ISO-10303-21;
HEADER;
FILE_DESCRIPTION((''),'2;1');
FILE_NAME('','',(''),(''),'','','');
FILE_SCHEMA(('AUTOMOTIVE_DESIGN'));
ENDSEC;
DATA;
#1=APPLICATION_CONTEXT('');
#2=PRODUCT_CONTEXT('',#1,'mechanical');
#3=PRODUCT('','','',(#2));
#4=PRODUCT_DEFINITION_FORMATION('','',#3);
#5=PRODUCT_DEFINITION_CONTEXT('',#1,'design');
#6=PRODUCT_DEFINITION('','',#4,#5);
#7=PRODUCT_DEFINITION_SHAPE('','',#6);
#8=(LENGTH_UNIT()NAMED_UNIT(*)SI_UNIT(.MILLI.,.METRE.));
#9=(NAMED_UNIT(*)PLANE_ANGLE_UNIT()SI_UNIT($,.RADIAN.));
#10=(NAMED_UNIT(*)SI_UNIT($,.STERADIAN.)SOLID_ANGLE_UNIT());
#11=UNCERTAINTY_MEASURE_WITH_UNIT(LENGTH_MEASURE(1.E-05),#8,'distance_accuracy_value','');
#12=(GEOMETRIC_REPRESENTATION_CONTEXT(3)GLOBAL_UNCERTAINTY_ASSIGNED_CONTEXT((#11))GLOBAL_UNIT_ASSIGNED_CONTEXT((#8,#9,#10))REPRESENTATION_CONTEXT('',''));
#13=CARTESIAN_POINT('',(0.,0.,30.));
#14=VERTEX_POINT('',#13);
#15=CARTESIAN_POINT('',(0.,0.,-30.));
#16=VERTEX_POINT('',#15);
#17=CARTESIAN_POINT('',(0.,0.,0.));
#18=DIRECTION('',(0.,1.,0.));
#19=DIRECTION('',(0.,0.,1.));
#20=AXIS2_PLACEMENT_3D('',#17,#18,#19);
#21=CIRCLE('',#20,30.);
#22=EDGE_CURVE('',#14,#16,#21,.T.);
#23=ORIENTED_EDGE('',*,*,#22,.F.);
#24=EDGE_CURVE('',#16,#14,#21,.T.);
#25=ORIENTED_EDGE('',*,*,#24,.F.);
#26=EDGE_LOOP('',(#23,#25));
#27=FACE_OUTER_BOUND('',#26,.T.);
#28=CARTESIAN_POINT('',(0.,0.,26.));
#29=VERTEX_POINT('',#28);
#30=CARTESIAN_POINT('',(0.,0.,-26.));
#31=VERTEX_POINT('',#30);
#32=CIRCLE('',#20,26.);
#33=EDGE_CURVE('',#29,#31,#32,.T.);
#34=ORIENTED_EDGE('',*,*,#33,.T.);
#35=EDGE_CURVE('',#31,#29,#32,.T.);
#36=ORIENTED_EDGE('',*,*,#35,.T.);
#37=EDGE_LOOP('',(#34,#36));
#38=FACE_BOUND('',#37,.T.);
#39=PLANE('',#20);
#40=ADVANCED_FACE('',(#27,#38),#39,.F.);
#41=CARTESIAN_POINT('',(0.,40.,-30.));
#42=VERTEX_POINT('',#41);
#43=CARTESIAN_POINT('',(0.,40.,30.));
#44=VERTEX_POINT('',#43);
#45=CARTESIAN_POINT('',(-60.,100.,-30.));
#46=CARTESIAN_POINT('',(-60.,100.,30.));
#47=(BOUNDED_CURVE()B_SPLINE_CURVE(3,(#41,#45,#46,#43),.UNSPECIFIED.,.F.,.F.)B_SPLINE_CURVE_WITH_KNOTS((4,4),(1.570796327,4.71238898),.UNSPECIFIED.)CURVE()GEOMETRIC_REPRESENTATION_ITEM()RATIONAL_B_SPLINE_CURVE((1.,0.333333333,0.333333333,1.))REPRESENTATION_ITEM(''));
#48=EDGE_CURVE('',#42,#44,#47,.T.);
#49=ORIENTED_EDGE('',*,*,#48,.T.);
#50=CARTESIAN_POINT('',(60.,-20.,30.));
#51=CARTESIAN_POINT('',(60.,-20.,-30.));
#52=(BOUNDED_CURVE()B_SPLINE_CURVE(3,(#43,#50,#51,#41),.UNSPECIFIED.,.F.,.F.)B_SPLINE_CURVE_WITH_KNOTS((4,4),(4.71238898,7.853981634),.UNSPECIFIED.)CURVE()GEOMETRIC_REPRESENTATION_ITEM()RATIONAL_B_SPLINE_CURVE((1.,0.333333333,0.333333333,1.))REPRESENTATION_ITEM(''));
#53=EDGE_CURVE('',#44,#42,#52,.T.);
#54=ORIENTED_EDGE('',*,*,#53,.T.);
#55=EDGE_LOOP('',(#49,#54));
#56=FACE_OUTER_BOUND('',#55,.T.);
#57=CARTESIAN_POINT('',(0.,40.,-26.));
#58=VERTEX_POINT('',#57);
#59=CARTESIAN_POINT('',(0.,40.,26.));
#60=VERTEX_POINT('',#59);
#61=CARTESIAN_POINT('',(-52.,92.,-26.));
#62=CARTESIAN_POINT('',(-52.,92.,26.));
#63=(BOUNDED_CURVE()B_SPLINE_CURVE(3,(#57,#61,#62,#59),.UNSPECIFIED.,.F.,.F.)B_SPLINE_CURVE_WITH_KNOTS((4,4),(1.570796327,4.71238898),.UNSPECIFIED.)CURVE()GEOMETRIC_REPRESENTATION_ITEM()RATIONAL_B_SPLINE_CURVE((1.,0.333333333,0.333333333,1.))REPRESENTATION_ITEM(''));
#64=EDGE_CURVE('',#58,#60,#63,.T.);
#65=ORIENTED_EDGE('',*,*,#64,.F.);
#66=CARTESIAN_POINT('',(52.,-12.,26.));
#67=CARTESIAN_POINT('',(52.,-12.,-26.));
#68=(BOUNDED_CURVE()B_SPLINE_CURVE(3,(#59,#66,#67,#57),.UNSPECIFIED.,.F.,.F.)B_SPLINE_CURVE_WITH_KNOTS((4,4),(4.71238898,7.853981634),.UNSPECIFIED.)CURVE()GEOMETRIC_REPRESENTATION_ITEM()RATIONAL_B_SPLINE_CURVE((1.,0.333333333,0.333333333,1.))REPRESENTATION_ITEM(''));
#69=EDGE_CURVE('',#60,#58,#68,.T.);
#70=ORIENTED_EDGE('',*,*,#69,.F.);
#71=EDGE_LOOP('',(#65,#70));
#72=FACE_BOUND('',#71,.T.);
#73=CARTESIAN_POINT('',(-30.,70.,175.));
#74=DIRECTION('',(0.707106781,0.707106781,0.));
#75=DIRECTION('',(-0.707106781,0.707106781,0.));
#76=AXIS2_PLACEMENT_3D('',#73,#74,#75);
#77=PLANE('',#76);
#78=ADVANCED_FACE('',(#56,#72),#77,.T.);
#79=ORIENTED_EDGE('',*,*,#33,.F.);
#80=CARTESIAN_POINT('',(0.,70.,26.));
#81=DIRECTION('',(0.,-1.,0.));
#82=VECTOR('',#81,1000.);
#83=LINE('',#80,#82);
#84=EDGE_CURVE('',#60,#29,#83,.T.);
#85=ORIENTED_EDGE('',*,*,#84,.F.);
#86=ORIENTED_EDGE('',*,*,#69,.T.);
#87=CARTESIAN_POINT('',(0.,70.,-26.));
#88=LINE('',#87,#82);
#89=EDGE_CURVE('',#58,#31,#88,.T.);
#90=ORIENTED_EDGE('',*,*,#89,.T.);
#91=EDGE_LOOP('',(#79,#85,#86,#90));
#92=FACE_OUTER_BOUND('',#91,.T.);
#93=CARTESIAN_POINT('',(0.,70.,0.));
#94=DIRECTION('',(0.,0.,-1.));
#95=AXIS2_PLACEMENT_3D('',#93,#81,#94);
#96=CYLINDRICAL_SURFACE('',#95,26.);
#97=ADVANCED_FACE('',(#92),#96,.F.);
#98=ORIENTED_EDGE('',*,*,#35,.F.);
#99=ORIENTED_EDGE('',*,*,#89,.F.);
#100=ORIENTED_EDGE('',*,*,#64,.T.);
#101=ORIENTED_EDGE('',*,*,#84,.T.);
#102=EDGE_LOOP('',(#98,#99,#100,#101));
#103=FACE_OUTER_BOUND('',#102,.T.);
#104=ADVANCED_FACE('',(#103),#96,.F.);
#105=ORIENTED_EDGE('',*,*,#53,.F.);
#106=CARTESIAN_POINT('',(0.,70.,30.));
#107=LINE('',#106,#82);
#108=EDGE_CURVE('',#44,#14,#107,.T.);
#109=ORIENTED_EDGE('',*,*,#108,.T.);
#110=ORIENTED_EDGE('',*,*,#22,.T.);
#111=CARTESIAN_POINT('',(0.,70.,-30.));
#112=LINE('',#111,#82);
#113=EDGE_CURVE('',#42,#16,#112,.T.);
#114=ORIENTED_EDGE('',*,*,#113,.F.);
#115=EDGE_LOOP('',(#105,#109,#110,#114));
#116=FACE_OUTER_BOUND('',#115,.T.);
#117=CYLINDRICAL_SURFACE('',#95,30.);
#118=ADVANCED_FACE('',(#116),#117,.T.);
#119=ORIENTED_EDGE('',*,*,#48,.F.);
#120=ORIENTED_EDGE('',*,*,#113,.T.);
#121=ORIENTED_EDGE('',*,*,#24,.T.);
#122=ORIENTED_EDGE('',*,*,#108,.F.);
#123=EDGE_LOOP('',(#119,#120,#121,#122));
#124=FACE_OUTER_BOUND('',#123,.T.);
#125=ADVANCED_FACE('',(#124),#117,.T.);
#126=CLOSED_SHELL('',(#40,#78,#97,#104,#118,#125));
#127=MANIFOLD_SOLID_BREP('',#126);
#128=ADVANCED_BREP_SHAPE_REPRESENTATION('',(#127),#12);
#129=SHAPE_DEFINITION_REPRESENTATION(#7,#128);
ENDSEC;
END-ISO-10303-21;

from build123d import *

# Parameters (mm, degrees)
SKETCH1_R               = 30
SKETCH1_R_2             = 26
BOSS_EXTRUDE1_DEPTH     = 70
CUT_EXTRUDE1_DEPTH      = 82.853527719
CUT_EXTRUDE1_DEPTH_BACK = 82.853527719


with BuildPart() as part:
    # Sketch1 → Boss-Extrude1 (new body)
    with BuildSketch(Plane(origin=(0, 0, 0), x_dir=(1, 0, 0), z_dir=(0, 1, 0))):
        with Locations(Location((0, 0, 0), (0, 0, 270))):
            Circle(SKETCH1_R)
        with Locations(Location((0, 0, 0), (0, 0, 270))):
            Circle(SKETCH1_R_2, mode=Mode.SUBTRACT)
    extrude(amount=BOSS_EXTRUDE1_DEPTH)

    # Sketch2 → Cut-Extrude1 (cut, two sides: drawn at the far end of the back side and taken through both)
    with BuildSketch(Plane.XY.offset(-CUT_EXTRUDE1_DEPTH_BACK)):
        Polygon((-167.455115916, 207.455115916), (-30, 70), (33.212319076, 6.787680924), (170.667434992, -130.667434992), (445.577666824, 144.24279684), (107.455115916, 482.365347748), align=None)
    extrude(amount=CUT_EXTRUDE1_DEPTH + CUT_EXTRUDE1_DEPTH_BACK, mode=Mode.SUBTRACT)


solid = part.part
